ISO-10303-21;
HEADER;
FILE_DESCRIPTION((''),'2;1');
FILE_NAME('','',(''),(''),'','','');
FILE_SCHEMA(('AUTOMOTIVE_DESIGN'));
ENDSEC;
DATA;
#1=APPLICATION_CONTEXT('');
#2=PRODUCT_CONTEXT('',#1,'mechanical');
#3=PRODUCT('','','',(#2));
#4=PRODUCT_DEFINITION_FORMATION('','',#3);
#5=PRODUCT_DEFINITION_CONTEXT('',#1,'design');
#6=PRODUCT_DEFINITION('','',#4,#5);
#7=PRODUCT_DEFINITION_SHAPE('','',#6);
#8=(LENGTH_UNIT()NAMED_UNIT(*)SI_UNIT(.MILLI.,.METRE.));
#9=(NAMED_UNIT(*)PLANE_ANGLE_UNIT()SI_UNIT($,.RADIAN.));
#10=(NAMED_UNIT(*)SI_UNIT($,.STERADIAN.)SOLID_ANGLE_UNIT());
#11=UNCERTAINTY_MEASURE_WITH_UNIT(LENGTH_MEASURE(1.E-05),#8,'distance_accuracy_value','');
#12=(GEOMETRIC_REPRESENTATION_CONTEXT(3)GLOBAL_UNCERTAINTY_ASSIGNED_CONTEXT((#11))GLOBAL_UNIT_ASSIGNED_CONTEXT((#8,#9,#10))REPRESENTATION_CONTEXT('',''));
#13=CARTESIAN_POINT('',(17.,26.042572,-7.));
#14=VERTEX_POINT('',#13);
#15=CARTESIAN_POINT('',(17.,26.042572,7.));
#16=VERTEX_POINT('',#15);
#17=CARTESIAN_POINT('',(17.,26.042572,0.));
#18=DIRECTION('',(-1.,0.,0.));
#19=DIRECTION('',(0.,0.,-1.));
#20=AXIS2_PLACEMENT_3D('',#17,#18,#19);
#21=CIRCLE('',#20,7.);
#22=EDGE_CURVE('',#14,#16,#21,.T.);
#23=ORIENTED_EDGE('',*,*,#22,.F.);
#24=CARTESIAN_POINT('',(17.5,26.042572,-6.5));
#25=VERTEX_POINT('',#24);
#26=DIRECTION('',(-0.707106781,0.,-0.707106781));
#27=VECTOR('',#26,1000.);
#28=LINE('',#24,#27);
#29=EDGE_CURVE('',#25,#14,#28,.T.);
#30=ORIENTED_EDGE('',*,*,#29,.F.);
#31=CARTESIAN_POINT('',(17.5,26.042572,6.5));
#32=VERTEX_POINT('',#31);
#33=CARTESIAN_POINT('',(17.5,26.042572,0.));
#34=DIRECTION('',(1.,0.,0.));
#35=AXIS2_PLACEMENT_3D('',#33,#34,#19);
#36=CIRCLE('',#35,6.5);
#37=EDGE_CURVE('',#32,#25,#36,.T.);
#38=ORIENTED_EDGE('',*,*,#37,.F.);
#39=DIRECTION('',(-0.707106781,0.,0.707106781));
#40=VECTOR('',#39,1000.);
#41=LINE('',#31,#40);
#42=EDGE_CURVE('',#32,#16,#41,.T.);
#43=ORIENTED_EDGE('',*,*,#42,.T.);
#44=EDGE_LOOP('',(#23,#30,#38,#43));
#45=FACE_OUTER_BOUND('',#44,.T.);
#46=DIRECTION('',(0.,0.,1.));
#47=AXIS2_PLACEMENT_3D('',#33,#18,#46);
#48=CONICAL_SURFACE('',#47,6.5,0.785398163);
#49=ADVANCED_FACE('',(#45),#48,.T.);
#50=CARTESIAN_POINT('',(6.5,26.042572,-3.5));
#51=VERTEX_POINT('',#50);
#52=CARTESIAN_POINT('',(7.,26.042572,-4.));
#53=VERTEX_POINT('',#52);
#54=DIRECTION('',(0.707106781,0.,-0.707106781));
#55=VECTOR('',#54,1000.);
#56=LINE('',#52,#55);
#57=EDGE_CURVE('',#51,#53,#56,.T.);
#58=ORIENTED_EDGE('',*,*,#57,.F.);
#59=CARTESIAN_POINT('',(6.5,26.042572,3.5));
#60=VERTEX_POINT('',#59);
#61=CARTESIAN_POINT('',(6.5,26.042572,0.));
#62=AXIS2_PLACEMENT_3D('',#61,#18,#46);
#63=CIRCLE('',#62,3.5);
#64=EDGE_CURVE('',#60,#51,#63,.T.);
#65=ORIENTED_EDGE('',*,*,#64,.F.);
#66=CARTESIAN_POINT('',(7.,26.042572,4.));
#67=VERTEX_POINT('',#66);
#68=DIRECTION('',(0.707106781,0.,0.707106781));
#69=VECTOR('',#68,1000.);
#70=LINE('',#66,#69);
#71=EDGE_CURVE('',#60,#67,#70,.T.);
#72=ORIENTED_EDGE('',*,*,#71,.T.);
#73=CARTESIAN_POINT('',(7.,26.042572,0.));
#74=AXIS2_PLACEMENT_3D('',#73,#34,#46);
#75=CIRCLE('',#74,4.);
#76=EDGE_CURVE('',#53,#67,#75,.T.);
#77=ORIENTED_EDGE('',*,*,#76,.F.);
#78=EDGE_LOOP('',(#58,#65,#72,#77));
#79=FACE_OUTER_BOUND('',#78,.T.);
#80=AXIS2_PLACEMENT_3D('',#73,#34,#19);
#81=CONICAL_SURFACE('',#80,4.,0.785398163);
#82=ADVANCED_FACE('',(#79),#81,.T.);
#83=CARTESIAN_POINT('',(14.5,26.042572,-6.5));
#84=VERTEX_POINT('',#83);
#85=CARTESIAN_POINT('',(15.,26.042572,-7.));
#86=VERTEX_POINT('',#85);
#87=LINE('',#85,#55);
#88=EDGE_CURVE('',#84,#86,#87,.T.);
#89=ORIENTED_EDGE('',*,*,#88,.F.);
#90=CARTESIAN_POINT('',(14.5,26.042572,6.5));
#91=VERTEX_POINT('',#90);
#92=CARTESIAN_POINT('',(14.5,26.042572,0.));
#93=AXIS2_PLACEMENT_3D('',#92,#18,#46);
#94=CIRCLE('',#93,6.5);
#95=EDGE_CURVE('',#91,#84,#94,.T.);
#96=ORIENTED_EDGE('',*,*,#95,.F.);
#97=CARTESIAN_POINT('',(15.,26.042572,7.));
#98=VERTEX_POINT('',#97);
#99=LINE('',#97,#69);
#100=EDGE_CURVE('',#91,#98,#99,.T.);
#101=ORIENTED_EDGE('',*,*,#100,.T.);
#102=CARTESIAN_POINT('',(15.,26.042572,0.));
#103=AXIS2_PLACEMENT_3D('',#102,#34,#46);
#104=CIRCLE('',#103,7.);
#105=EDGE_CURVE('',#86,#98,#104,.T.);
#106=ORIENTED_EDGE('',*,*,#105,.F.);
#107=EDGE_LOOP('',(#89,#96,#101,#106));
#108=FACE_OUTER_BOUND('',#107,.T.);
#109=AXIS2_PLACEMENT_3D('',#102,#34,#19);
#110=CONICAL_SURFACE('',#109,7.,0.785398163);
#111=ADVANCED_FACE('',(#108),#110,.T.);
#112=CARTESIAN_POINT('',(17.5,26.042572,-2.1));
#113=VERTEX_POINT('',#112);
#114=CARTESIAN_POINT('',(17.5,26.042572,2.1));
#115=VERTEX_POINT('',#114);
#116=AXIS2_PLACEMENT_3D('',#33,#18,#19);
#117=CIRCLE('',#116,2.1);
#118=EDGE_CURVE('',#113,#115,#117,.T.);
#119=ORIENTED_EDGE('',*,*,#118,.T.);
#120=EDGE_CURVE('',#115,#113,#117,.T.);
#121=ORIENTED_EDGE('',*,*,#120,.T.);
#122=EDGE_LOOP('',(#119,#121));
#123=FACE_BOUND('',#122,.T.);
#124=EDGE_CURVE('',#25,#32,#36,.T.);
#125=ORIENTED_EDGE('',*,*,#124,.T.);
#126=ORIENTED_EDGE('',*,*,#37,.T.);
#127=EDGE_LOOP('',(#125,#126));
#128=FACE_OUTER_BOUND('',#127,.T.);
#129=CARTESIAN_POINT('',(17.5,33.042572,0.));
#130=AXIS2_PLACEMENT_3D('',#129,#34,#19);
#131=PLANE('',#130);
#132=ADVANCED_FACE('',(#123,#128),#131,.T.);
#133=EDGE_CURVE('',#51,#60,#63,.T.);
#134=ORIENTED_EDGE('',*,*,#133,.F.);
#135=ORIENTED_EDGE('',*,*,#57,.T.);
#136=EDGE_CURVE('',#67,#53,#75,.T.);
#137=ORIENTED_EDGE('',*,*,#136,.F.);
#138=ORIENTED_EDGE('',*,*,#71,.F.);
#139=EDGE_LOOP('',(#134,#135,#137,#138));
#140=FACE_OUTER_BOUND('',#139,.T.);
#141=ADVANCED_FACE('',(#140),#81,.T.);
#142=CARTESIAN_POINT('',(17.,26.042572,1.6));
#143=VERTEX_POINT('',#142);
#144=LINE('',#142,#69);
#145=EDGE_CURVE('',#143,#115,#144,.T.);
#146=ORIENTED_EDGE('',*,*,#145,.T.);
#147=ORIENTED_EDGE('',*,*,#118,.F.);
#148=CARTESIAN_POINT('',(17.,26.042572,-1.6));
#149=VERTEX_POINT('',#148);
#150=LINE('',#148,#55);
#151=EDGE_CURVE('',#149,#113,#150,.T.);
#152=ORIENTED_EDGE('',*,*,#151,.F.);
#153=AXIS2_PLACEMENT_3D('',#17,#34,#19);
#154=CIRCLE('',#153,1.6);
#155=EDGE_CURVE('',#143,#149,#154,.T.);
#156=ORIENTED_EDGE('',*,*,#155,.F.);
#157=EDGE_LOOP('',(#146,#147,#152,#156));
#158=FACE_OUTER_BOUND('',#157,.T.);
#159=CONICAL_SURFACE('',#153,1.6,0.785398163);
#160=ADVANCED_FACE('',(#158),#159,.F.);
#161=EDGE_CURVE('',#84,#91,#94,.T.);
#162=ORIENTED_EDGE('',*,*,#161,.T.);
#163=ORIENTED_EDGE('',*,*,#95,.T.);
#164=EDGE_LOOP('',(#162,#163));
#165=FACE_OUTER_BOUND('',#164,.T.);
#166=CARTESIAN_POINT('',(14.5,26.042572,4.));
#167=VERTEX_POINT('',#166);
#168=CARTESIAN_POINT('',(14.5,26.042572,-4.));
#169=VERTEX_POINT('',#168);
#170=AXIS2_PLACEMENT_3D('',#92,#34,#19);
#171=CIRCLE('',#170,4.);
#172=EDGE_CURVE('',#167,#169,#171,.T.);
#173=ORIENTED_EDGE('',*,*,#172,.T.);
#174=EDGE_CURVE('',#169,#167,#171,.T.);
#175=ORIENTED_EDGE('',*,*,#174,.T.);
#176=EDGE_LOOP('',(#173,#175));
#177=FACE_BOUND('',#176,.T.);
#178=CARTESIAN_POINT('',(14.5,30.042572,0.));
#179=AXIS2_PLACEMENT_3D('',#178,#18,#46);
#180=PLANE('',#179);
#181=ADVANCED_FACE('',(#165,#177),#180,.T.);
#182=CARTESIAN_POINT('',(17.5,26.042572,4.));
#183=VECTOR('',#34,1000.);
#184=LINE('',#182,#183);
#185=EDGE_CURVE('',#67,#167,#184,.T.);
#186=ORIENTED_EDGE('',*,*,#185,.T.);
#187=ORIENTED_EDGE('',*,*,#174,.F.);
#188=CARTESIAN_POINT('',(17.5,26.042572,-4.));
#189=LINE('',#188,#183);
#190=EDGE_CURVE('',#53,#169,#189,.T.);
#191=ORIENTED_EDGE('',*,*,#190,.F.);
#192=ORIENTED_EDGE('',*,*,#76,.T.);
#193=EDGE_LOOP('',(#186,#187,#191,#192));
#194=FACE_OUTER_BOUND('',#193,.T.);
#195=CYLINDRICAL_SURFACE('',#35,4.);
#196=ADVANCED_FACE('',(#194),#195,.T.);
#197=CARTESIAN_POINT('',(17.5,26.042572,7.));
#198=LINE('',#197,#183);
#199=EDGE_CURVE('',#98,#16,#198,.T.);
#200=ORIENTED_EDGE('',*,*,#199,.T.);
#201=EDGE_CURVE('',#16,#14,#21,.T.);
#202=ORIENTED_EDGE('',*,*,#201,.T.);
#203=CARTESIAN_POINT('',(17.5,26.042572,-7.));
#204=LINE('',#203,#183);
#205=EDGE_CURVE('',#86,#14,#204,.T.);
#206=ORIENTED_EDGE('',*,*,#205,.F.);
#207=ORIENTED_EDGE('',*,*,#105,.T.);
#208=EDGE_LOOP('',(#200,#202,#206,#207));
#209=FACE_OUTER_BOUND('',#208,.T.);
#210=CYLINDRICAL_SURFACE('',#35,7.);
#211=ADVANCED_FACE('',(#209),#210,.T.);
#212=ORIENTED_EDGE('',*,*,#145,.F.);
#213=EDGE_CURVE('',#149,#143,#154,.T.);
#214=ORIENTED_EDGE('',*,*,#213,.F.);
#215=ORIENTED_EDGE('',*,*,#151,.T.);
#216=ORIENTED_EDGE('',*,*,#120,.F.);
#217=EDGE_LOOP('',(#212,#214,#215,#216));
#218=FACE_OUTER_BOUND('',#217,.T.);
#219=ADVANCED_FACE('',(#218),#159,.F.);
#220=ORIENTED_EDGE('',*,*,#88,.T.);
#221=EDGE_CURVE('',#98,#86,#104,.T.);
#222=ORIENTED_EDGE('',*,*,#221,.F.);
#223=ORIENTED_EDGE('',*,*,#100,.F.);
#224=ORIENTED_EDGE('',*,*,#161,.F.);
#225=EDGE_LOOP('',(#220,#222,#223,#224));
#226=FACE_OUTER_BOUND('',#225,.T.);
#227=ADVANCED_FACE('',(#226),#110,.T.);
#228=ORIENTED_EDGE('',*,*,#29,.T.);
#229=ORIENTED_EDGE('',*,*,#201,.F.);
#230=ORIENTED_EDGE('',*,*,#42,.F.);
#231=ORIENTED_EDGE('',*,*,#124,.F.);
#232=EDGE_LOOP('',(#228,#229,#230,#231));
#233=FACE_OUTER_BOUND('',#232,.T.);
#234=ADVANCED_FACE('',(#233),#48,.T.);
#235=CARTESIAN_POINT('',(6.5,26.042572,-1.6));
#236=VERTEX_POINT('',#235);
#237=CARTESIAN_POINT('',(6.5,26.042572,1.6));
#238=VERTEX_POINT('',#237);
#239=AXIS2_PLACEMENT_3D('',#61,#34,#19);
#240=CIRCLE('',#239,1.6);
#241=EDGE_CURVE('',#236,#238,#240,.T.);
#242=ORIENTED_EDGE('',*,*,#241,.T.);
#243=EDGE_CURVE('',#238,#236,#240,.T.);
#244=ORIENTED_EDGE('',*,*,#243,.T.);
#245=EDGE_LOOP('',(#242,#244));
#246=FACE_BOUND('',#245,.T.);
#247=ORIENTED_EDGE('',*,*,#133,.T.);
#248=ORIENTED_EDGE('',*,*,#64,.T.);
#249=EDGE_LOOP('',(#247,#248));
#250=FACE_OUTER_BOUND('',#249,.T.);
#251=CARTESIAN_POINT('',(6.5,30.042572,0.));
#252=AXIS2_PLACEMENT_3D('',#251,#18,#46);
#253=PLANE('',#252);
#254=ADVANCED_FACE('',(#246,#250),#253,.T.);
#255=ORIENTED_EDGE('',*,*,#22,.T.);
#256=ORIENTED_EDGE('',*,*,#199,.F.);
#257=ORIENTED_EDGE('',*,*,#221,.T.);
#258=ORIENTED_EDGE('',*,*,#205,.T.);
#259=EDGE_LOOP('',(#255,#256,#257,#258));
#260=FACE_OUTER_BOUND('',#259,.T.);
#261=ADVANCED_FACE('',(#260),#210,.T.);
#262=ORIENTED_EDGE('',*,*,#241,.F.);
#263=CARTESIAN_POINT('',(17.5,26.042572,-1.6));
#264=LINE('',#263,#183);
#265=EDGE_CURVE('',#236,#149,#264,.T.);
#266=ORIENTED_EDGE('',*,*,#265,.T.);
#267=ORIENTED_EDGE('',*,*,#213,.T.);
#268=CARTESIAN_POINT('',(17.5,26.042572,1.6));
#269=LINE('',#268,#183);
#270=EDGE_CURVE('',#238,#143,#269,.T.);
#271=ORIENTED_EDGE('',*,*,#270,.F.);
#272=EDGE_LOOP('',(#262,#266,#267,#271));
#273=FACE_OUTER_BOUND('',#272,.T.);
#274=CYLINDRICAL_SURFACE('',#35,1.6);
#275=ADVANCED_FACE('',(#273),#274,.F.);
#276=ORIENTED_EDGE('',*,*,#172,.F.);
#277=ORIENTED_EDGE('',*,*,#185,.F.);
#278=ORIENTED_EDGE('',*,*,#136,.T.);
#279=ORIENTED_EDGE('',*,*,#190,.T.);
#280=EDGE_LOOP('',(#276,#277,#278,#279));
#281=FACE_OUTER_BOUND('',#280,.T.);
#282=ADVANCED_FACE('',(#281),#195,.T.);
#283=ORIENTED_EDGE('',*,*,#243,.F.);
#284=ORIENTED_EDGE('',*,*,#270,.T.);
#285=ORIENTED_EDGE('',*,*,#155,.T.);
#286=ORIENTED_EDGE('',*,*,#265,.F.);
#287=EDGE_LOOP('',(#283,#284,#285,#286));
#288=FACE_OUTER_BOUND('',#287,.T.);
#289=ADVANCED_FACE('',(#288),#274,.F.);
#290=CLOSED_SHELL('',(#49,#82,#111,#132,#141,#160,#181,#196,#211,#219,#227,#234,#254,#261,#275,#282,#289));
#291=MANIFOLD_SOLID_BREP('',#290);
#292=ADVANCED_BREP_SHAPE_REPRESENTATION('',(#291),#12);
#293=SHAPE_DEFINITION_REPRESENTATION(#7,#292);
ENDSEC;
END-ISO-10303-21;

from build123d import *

# Parameters (mm, degrees)
CHAMFER1_SIZE = 0.5


with BuildPart() as part:
    # Sketch1 → Revolve1 (revolve)
    with BuildSketch(Plane.XY, mode=Mode.PRIVATE) as revolve1_sk:
        Polygon((6.5, 30.042572215), (14.5, 30.042572215), (14.5, 33.042572215), (17.5, 33.042572215), (17.5, 27.642572215), (6.5, 27.642572215), align=None)
    revolve(revolve1_sk.sketch.rotate(Axis((17.5, 26.042572215, 0), (-1, 0, 0)), 90), axis=Axis((17.5, 26.042572215, 0), (-1, 0, 0)))

    # Chamfer1
    chamfer1_edges = [part.edges().sort_by_distance(p)[0] for p in [
        (17.5, 26.042572215, 7),
        (14.5, 26.042572215, 7),
        (6.5, 26.042572215, 4),
        (17.5, 26.042572215, 1.6),
    ]]
    chamfer(chamfer1_edges, length=CHAMFER1_SIZE)


solid = part.part
